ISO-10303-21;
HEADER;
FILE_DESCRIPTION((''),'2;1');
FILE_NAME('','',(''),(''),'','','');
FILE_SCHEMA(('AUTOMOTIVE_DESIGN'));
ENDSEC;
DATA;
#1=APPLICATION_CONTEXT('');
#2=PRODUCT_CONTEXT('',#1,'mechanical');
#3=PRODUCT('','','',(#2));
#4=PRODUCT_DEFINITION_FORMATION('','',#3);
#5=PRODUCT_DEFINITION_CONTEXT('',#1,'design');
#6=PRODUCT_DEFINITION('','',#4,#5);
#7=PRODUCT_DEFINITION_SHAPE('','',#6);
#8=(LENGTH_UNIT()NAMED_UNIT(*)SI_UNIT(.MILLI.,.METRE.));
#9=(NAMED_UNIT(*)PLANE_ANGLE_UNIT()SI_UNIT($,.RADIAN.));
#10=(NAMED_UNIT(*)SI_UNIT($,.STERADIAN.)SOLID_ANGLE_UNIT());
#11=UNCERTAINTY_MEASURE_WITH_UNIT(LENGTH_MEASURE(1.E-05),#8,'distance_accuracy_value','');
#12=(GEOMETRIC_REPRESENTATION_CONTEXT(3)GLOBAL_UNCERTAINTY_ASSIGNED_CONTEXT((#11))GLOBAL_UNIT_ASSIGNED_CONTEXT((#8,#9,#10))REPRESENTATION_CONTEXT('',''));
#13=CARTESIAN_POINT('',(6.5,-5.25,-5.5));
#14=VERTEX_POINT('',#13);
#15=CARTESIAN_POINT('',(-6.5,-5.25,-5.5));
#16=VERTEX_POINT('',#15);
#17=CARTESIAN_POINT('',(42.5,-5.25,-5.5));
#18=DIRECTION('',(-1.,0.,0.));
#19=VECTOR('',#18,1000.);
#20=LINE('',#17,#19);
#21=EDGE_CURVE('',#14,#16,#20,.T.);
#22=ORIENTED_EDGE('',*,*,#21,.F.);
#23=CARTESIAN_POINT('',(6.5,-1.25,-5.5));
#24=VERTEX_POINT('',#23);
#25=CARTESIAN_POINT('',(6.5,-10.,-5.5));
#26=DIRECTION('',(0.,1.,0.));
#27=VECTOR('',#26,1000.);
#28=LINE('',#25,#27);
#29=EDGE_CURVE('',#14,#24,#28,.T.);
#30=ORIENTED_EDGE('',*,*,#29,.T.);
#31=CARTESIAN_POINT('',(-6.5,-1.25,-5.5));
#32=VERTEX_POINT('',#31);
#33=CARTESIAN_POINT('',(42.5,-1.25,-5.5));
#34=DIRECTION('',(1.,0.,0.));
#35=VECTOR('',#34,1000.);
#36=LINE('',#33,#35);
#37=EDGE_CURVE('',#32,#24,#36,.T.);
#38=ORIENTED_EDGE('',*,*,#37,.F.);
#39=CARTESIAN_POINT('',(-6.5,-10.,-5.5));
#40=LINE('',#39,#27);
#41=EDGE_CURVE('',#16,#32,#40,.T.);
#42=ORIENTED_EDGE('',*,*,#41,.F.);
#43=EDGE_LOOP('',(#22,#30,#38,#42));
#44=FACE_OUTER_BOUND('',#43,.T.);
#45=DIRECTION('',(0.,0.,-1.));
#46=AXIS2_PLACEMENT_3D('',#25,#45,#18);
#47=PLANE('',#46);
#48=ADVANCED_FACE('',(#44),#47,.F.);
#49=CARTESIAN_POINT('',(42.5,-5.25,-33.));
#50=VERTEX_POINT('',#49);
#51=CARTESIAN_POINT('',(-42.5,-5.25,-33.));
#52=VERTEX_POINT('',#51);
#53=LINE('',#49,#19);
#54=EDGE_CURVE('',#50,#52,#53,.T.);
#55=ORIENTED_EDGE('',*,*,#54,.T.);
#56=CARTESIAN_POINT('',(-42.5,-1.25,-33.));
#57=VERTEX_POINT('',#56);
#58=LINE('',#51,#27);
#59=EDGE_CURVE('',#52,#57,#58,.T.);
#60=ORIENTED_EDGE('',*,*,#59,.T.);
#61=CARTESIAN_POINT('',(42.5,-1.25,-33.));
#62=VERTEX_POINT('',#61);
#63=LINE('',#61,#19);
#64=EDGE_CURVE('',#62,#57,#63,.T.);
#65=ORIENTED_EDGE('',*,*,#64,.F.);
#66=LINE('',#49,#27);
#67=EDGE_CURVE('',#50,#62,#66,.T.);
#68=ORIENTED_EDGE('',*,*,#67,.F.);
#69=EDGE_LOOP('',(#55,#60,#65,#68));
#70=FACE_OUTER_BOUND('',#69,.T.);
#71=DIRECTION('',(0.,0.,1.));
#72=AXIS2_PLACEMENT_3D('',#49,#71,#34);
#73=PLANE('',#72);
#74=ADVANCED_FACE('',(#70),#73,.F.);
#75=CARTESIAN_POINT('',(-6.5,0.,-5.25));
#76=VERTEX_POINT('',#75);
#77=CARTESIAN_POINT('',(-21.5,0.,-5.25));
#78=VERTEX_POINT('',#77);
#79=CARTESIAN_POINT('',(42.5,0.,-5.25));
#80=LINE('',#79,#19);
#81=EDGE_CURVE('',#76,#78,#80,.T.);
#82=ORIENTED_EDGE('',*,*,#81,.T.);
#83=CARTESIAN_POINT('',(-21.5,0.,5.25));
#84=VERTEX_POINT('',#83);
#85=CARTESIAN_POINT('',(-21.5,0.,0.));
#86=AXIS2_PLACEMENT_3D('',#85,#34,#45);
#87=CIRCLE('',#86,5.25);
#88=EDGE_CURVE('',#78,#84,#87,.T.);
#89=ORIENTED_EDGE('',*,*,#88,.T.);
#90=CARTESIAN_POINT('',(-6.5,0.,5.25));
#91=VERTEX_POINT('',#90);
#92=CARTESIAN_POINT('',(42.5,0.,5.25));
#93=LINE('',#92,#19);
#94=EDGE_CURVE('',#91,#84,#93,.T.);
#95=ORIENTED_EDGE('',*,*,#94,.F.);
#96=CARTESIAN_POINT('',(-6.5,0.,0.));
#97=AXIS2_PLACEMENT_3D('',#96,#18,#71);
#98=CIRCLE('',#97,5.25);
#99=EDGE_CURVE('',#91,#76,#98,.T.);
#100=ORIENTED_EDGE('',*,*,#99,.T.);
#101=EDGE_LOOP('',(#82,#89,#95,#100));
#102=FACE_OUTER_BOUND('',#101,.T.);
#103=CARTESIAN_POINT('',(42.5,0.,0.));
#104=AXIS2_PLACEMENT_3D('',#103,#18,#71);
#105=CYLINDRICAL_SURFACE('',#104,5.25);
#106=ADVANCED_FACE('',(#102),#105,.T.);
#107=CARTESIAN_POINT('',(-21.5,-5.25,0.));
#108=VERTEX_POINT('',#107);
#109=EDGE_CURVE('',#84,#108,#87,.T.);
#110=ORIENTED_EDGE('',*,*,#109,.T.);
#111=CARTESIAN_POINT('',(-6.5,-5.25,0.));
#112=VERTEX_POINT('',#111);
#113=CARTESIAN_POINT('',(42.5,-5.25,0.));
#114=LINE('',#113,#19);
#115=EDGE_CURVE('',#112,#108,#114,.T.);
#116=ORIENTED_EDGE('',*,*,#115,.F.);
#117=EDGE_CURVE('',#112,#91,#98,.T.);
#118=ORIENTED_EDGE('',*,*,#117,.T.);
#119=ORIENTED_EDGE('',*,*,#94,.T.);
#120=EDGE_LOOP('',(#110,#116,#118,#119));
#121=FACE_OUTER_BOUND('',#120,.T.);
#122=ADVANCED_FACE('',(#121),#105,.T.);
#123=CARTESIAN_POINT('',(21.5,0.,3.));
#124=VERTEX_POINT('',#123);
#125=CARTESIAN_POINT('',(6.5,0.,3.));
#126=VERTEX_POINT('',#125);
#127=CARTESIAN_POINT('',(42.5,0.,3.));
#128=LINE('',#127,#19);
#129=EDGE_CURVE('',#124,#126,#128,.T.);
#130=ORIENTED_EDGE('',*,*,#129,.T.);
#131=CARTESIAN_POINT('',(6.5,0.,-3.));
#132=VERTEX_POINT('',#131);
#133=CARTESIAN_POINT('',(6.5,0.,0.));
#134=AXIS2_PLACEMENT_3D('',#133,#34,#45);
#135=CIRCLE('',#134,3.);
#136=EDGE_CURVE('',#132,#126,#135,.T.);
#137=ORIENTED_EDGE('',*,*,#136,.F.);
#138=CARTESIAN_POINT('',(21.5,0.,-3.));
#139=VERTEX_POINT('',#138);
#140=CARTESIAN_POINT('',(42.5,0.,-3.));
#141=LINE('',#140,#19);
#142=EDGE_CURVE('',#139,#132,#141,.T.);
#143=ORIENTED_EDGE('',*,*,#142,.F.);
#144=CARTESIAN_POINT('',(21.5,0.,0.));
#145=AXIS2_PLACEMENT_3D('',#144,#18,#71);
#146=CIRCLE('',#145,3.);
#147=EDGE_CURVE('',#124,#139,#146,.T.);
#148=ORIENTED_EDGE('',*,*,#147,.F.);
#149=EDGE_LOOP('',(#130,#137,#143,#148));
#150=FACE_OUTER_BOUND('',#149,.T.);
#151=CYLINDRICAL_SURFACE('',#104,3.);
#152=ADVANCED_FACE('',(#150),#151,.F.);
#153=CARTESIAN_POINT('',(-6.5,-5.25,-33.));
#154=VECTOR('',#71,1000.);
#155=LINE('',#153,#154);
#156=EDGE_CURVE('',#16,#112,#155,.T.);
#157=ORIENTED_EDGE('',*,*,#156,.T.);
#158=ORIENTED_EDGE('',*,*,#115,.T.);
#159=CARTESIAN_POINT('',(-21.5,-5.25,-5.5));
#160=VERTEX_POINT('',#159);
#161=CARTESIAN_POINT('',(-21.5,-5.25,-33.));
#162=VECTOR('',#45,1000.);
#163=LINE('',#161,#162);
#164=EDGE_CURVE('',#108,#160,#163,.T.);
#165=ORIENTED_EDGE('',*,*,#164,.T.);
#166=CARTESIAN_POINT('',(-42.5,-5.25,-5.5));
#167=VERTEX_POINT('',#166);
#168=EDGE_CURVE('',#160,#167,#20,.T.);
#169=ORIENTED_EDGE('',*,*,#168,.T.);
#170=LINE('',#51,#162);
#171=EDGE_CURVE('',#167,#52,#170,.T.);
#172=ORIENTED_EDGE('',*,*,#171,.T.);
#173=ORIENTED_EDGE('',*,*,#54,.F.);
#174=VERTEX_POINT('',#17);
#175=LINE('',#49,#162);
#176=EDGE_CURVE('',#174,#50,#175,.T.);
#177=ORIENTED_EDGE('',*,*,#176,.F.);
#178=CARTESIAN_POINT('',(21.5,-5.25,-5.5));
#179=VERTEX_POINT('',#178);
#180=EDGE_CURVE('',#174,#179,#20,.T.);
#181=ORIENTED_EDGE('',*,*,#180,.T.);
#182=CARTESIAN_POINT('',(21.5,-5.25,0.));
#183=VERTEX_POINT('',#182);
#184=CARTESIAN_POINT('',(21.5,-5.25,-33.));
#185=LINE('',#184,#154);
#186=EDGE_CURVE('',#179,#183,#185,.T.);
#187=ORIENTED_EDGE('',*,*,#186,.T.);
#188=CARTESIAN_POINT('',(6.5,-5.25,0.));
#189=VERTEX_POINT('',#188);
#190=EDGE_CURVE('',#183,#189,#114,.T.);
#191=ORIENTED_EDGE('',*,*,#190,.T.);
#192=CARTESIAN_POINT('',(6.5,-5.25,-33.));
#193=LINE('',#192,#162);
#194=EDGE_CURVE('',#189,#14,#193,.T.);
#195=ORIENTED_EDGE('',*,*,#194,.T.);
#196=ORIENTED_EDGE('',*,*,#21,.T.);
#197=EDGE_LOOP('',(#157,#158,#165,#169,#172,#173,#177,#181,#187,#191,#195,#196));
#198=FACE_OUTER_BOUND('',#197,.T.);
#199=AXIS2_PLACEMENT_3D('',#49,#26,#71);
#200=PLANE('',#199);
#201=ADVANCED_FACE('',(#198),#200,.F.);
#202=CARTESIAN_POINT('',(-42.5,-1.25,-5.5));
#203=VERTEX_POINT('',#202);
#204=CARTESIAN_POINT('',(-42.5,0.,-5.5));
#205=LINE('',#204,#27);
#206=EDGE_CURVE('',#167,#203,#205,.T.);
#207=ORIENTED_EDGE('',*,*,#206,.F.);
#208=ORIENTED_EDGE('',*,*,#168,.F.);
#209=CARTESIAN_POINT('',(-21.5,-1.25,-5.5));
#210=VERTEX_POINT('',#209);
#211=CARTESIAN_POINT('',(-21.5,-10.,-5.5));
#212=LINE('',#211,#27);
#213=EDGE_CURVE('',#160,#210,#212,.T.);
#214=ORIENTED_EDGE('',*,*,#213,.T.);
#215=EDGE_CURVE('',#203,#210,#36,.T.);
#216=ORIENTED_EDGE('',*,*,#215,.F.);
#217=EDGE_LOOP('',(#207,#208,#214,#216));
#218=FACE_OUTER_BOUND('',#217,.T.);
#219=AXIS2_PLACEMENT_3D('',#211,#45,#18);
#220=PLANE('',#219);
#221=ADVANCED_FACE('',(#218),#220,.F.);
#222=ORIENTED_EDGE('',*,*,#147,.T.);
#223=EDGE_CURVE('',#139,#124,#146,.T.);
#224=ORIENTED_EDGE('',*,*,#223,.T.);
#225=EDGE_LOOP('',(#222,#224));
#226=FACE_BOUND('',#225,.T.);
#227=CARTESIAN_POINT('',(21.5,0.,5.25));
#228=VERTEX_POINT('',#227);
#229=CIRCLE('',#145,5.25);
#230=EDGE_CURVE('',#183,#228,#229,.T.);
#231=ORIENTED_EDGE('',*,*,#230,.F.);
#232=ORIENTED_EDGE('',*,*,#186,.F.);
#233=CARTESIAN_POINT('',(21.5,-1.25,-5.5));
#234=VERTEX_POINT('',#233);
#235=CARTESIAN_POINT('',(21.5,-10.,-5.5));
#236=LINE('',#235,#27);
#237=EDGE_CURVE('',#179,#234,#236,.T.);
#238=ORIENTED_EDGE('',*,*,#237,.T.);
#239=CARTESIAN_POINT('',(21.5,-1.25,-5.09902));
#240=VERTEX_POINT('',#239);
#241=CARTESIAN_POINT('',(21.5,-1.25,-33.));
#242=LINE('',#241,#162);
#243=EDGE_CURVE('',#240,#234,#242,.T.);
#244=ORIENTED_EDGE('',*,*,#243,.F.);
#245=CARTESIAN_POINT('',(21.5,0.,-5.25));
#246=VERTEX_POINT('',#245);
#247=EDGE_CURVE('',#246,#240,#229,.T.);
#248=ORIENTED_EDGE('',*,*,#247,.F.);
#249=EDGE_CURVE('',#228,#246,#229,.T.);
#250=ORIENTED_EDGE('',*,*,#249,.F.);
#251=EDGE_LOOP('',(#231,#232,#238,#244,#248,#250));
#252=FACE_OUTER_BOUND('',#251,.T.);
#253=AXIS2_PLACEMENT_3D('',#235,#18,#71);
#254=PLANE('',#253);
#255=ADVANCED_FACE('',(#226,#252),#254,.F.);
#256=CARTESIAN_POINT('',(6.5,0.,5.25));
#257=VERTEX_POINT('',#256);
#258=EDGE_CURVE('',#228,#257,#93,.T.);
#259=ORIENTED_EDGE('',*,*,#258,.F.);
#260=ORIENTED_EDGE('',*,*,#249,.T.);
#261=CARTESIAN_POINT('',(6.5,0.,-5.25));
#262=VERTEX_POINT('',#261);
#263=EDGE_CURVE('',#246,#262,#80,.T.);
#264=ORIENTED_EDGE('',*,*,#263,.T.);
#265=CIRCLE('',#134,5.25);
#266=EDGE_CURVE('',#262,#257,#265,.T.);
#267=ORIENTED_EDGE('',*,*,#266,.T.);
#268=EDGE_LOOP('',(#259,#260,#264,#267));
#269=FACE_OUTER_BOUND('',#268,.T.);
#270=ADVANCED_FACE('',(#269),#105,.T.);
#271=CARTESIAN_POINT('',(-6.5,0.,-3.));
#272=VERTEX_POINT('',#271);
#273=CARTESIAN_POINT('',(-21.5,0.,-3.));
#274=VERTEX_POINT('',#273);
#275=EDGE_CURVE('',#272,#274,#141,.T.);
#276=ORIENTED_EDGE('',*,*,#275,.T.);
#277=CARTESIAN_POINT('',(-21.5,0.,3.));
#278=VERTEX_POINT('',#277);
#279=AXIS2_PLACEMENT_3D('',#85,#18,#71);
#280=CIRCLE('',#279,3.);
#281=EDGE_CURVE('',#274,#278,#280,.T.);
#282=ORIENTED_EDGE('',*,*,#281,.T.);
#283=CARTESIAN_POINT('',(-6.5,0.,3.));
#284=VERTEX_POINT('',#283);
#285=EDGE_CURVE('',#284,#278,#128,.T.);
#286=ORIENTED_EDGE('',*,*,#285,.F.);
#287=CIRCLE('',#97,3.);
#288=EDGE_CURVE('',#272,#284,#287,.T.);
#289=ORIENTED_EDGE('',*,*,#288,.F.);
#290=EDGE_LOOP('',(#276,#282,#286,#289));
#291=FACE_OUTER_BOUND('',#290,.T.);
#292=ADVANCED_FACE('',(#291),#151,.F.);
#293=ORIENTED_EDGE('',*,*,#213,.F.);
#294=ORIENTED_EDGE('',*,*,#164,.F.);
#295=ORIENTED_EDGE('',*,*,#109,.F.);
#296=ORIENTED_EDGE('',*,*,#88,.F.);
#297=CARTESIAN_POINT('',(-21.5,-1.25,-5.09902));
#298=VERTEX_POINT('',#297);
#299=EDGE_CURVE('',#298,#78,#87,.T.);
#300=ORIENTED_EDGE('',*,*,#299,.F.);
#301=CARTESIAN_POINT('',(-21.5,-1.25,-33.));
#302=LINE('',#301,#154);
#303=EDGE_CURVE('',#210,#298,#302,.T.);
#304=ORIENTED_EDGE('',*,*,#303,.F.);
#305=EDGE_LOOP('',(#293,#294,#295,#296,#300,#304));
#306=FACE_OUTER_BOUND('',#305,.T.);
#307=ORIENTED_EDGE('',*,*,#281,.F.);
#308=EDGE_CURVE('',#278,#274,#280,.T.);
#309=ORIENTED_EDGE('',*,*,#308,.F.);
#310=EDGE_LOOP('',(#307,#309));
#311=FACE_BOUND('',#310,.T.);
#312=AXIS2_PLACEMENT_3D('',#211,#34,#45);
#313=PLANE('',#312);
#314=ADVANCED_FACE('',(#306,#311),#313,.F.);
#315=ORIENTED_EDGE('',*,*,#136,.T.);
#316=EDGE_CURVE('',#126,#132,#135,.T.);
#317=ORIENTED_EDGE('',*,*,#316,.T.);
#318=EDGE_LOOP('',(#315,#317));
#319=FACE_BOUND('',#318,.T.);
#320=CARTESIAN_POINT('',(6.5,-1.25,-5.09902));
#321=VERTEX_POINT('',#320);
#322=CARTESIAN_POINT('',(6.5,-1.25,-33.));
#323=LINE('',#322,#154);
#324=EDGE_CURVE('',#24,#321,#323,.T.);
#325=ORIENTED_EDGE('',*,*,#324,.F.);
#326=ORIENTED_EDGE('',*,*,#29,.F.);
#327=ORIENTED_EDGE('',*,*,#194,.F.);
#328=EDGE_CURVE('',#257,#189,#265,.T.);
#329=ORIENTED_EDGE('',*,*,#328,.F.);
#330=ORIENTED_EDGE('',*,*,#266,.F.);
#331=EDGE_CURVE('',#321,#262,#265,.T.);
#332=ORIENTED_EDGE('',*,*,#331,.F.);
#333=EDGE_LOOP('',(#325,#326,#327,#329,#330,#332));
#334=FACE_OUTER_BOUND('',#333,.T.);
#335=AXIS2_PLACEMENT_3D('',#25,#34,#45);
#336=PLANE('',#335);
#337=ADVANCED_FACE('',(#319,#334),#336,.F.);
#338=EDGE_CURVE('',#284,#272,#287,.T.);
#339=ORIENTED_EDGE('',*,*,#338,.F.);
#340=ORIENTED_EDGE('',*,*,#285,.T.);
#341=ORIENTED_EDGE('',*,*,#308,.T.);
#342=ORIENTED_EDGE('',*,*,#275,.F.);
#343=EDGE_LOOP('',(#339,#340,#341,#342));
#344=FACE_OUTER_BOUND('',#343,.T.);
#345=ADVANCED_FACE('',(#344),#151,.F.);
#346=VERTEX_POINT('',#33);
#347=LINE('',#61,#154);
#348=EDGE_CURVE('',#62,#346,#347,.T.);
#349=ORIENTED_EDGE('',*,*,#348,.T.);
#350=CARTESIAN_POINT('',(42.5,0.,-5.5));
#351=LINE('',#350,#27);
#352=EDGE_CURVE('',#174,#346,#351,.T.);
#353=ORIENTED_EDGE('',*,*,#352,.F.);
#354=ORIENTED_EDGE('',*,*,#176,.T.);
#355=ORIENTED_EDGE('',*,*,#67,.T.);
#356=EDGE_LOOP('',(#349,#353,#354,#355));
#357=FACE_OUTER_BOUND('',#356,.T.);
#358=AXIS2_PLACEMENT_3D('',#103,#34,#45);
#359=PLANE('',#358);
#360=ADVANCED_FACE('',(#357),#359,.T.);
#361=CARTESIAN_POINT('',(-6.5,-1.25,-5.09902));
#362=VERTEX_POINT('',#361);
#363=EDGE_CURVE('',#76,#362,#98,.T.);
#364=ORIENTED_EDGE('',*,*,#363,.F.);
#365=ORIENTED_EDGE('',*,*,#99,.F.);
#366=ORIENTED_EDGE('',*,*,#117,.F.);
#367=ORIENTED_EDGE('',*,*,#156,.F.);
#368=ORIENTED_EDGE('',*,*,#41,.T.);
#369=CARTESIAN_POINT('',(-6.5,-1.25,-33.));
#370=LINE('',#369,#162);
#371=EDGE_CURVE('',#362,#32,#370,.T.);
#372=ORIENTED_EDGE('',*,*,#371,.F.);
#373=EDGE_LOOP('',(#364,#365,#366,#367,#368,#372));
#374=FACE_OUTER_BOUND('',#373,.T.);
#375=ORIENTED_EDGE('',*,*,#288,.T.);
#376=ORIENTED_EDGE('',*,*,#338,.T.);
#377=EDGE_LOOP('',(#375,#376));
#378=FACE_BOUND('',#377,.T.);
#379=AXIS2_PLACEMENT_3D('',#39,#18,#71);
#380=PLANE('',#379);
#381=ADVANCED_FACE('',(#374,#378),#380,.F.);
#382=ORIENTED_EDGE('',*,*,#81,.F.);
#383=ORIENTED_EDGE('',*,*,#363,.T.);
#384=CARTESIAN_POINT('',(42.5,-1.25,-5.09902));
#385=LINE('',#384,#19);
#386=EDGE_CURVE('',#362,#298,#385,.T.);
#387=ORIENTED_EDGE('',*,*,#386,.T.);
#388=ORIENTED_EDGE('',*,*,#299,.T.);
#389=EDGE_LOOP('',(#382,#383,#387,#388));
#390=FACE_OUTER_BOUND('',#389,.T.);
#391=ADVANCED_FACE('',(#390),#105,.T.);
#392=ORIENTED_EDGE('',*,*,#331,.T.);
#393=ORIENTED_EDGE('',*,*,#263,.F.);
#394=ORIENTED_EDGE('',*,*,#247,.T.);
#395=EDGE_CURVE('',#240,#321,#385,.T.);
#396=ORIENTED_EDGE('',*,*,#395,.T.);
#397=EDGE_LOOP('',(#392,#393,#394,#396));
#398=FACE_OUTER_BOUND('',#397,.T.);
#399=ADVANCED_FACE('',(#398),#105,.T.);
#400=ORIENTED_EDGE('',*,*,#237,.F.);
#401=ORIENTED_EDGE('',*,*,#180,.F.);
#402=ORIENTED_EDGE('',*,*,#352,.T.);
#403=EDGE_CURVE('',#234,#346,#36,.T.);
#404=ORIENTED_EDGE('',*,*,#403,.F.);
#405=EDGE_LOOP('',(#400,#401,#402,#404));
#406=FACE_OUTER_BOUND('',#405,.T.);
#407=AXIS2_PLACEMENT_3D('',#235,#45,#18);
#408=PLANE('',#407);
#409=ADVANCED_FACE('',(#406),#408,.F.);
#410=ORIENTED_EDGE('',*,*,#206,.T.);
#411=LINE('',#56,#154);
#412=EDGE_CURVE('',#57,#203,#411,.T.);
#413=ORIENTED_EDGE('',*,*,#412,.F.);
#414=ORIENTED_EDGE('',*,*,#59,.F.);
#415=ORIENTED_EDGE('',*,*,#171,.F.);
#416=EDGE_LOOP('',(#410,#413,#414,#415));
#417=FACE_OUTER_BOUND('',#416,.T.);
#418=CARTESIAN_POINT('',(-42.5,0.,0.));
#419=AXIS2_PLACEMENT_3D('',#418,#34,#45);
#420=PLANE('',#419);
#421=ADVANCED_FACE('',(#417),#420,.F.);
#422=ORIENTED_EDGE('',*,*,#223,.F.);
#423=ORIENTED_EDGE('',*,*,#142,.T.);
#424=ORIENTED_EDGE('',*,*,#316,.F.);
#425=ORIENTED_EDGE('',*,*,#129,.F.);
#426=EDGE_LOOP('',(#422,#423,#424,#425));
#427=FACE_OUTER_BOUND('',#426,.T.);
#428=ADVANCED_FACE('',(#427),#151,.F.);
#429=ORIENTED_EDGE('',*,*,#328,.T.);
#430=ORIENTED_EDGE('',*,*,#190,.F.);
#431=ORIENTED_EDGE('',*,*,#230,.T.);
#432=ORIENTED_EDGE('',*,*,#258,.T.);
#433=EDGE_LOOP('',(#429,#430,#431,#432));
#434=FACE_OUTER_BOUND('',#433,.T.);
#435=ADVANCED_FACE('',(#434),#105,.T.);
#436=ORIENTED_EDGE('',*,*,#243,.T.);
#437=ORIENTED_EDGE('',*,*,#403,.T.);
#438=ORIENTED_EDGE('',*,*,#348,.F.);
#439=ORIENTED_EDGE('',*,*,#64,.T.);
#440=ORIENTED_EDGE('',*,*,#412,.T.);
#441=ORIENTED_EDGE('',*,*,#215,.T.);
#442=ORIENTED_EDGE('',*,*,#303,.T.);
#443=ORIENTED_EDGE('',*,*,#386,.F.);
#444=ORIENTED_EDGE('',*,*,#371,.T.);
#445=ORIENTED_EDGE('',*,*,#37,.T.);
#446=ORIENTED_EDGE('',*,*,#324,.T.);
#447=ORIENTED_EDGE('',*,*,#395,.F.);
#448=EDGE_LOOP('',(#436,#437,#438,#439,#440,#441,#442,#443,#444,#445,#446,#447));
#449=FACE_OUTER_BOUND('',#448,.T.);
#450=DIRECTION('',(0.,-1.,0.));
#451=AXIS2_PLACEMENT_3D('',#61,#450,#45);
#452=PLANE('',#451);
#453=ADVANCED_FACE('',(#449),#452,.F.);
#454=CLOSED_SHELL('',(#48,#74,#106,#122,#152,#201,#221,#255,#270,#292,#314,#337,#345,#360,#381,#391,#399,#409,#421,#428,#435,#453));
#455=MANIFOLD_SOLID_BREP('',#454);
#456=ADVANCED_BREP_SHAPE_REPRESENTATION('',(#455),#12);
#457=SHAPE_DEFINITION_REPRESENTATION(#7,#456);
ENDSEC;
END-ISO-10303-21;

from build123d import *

# Parameters (mm, degrees)
BOSS_EXTRUDE1_DEPTH = 42.5
SKETCH3_W           = 13
SKETCH3_H           = 11
SKETCH3_W_2         = 21
SKETCH3_H_2         = 10.75
CUT_EXTRUDE2_DEPTH  = 10
SKETCH4_R           = 3
CUT_EXTRUDE3_DEPTH  = 73.198078229


with BuildPart() as part:
    # Sketch1 → Boss-Extrude1 (new, symmetric)
    with BuildSketch(Plane(origin=(0, 0, 0), x_dir=(0, 0, -1), z_dir=(1, 0, 0))):
        with BuildLine():
            Line((33, -5.25), (0, -5.25))
            ThreePointArc((0, -5.25), (-3.240370349, 4.13067791), (5.099019514, -1.25))
            Line((5.099019514, -1.25), (33, -1.25))
            Line((33, -1.25), (33, -5.25))
        make_face()
    extrude(amount=BOSS_EXTRUDE1_DEPTH, both=True)

    # Sketch3 → Cut-Extrude2 (cut, symmetric)
    with BuildSketch(Plane(origin=(0, 0, 0), x_dir=(1, 0, 0), z_dir=(0, 1, 0))):
        Rectangle(SKETCH3_W, SKETCH3_H)
        with Locations((32, 0.125)):
            Rectangle(SKETCH3_W_2, SKETCH3_H_2)
        with Locations((-32, 0.125)):
            Rectangle(SKETCH3_W_2, SKETCH3_H_2)
    extrude(amount=CUT_EXTRUDE2_DEPTH, both=True, mode=Mode.SUBTRACT)

    # Sketch4 → Cut-Extrude3 (cut, through all)
    with BuildSketch(Plane.ZY.offset(21.5)):
        Circle(SKETCH4_R)
    extrude(amount=-CUT_EXTRUDE3_DEPTH, mode=Mode.SUBTRACT)


solid = part.part
